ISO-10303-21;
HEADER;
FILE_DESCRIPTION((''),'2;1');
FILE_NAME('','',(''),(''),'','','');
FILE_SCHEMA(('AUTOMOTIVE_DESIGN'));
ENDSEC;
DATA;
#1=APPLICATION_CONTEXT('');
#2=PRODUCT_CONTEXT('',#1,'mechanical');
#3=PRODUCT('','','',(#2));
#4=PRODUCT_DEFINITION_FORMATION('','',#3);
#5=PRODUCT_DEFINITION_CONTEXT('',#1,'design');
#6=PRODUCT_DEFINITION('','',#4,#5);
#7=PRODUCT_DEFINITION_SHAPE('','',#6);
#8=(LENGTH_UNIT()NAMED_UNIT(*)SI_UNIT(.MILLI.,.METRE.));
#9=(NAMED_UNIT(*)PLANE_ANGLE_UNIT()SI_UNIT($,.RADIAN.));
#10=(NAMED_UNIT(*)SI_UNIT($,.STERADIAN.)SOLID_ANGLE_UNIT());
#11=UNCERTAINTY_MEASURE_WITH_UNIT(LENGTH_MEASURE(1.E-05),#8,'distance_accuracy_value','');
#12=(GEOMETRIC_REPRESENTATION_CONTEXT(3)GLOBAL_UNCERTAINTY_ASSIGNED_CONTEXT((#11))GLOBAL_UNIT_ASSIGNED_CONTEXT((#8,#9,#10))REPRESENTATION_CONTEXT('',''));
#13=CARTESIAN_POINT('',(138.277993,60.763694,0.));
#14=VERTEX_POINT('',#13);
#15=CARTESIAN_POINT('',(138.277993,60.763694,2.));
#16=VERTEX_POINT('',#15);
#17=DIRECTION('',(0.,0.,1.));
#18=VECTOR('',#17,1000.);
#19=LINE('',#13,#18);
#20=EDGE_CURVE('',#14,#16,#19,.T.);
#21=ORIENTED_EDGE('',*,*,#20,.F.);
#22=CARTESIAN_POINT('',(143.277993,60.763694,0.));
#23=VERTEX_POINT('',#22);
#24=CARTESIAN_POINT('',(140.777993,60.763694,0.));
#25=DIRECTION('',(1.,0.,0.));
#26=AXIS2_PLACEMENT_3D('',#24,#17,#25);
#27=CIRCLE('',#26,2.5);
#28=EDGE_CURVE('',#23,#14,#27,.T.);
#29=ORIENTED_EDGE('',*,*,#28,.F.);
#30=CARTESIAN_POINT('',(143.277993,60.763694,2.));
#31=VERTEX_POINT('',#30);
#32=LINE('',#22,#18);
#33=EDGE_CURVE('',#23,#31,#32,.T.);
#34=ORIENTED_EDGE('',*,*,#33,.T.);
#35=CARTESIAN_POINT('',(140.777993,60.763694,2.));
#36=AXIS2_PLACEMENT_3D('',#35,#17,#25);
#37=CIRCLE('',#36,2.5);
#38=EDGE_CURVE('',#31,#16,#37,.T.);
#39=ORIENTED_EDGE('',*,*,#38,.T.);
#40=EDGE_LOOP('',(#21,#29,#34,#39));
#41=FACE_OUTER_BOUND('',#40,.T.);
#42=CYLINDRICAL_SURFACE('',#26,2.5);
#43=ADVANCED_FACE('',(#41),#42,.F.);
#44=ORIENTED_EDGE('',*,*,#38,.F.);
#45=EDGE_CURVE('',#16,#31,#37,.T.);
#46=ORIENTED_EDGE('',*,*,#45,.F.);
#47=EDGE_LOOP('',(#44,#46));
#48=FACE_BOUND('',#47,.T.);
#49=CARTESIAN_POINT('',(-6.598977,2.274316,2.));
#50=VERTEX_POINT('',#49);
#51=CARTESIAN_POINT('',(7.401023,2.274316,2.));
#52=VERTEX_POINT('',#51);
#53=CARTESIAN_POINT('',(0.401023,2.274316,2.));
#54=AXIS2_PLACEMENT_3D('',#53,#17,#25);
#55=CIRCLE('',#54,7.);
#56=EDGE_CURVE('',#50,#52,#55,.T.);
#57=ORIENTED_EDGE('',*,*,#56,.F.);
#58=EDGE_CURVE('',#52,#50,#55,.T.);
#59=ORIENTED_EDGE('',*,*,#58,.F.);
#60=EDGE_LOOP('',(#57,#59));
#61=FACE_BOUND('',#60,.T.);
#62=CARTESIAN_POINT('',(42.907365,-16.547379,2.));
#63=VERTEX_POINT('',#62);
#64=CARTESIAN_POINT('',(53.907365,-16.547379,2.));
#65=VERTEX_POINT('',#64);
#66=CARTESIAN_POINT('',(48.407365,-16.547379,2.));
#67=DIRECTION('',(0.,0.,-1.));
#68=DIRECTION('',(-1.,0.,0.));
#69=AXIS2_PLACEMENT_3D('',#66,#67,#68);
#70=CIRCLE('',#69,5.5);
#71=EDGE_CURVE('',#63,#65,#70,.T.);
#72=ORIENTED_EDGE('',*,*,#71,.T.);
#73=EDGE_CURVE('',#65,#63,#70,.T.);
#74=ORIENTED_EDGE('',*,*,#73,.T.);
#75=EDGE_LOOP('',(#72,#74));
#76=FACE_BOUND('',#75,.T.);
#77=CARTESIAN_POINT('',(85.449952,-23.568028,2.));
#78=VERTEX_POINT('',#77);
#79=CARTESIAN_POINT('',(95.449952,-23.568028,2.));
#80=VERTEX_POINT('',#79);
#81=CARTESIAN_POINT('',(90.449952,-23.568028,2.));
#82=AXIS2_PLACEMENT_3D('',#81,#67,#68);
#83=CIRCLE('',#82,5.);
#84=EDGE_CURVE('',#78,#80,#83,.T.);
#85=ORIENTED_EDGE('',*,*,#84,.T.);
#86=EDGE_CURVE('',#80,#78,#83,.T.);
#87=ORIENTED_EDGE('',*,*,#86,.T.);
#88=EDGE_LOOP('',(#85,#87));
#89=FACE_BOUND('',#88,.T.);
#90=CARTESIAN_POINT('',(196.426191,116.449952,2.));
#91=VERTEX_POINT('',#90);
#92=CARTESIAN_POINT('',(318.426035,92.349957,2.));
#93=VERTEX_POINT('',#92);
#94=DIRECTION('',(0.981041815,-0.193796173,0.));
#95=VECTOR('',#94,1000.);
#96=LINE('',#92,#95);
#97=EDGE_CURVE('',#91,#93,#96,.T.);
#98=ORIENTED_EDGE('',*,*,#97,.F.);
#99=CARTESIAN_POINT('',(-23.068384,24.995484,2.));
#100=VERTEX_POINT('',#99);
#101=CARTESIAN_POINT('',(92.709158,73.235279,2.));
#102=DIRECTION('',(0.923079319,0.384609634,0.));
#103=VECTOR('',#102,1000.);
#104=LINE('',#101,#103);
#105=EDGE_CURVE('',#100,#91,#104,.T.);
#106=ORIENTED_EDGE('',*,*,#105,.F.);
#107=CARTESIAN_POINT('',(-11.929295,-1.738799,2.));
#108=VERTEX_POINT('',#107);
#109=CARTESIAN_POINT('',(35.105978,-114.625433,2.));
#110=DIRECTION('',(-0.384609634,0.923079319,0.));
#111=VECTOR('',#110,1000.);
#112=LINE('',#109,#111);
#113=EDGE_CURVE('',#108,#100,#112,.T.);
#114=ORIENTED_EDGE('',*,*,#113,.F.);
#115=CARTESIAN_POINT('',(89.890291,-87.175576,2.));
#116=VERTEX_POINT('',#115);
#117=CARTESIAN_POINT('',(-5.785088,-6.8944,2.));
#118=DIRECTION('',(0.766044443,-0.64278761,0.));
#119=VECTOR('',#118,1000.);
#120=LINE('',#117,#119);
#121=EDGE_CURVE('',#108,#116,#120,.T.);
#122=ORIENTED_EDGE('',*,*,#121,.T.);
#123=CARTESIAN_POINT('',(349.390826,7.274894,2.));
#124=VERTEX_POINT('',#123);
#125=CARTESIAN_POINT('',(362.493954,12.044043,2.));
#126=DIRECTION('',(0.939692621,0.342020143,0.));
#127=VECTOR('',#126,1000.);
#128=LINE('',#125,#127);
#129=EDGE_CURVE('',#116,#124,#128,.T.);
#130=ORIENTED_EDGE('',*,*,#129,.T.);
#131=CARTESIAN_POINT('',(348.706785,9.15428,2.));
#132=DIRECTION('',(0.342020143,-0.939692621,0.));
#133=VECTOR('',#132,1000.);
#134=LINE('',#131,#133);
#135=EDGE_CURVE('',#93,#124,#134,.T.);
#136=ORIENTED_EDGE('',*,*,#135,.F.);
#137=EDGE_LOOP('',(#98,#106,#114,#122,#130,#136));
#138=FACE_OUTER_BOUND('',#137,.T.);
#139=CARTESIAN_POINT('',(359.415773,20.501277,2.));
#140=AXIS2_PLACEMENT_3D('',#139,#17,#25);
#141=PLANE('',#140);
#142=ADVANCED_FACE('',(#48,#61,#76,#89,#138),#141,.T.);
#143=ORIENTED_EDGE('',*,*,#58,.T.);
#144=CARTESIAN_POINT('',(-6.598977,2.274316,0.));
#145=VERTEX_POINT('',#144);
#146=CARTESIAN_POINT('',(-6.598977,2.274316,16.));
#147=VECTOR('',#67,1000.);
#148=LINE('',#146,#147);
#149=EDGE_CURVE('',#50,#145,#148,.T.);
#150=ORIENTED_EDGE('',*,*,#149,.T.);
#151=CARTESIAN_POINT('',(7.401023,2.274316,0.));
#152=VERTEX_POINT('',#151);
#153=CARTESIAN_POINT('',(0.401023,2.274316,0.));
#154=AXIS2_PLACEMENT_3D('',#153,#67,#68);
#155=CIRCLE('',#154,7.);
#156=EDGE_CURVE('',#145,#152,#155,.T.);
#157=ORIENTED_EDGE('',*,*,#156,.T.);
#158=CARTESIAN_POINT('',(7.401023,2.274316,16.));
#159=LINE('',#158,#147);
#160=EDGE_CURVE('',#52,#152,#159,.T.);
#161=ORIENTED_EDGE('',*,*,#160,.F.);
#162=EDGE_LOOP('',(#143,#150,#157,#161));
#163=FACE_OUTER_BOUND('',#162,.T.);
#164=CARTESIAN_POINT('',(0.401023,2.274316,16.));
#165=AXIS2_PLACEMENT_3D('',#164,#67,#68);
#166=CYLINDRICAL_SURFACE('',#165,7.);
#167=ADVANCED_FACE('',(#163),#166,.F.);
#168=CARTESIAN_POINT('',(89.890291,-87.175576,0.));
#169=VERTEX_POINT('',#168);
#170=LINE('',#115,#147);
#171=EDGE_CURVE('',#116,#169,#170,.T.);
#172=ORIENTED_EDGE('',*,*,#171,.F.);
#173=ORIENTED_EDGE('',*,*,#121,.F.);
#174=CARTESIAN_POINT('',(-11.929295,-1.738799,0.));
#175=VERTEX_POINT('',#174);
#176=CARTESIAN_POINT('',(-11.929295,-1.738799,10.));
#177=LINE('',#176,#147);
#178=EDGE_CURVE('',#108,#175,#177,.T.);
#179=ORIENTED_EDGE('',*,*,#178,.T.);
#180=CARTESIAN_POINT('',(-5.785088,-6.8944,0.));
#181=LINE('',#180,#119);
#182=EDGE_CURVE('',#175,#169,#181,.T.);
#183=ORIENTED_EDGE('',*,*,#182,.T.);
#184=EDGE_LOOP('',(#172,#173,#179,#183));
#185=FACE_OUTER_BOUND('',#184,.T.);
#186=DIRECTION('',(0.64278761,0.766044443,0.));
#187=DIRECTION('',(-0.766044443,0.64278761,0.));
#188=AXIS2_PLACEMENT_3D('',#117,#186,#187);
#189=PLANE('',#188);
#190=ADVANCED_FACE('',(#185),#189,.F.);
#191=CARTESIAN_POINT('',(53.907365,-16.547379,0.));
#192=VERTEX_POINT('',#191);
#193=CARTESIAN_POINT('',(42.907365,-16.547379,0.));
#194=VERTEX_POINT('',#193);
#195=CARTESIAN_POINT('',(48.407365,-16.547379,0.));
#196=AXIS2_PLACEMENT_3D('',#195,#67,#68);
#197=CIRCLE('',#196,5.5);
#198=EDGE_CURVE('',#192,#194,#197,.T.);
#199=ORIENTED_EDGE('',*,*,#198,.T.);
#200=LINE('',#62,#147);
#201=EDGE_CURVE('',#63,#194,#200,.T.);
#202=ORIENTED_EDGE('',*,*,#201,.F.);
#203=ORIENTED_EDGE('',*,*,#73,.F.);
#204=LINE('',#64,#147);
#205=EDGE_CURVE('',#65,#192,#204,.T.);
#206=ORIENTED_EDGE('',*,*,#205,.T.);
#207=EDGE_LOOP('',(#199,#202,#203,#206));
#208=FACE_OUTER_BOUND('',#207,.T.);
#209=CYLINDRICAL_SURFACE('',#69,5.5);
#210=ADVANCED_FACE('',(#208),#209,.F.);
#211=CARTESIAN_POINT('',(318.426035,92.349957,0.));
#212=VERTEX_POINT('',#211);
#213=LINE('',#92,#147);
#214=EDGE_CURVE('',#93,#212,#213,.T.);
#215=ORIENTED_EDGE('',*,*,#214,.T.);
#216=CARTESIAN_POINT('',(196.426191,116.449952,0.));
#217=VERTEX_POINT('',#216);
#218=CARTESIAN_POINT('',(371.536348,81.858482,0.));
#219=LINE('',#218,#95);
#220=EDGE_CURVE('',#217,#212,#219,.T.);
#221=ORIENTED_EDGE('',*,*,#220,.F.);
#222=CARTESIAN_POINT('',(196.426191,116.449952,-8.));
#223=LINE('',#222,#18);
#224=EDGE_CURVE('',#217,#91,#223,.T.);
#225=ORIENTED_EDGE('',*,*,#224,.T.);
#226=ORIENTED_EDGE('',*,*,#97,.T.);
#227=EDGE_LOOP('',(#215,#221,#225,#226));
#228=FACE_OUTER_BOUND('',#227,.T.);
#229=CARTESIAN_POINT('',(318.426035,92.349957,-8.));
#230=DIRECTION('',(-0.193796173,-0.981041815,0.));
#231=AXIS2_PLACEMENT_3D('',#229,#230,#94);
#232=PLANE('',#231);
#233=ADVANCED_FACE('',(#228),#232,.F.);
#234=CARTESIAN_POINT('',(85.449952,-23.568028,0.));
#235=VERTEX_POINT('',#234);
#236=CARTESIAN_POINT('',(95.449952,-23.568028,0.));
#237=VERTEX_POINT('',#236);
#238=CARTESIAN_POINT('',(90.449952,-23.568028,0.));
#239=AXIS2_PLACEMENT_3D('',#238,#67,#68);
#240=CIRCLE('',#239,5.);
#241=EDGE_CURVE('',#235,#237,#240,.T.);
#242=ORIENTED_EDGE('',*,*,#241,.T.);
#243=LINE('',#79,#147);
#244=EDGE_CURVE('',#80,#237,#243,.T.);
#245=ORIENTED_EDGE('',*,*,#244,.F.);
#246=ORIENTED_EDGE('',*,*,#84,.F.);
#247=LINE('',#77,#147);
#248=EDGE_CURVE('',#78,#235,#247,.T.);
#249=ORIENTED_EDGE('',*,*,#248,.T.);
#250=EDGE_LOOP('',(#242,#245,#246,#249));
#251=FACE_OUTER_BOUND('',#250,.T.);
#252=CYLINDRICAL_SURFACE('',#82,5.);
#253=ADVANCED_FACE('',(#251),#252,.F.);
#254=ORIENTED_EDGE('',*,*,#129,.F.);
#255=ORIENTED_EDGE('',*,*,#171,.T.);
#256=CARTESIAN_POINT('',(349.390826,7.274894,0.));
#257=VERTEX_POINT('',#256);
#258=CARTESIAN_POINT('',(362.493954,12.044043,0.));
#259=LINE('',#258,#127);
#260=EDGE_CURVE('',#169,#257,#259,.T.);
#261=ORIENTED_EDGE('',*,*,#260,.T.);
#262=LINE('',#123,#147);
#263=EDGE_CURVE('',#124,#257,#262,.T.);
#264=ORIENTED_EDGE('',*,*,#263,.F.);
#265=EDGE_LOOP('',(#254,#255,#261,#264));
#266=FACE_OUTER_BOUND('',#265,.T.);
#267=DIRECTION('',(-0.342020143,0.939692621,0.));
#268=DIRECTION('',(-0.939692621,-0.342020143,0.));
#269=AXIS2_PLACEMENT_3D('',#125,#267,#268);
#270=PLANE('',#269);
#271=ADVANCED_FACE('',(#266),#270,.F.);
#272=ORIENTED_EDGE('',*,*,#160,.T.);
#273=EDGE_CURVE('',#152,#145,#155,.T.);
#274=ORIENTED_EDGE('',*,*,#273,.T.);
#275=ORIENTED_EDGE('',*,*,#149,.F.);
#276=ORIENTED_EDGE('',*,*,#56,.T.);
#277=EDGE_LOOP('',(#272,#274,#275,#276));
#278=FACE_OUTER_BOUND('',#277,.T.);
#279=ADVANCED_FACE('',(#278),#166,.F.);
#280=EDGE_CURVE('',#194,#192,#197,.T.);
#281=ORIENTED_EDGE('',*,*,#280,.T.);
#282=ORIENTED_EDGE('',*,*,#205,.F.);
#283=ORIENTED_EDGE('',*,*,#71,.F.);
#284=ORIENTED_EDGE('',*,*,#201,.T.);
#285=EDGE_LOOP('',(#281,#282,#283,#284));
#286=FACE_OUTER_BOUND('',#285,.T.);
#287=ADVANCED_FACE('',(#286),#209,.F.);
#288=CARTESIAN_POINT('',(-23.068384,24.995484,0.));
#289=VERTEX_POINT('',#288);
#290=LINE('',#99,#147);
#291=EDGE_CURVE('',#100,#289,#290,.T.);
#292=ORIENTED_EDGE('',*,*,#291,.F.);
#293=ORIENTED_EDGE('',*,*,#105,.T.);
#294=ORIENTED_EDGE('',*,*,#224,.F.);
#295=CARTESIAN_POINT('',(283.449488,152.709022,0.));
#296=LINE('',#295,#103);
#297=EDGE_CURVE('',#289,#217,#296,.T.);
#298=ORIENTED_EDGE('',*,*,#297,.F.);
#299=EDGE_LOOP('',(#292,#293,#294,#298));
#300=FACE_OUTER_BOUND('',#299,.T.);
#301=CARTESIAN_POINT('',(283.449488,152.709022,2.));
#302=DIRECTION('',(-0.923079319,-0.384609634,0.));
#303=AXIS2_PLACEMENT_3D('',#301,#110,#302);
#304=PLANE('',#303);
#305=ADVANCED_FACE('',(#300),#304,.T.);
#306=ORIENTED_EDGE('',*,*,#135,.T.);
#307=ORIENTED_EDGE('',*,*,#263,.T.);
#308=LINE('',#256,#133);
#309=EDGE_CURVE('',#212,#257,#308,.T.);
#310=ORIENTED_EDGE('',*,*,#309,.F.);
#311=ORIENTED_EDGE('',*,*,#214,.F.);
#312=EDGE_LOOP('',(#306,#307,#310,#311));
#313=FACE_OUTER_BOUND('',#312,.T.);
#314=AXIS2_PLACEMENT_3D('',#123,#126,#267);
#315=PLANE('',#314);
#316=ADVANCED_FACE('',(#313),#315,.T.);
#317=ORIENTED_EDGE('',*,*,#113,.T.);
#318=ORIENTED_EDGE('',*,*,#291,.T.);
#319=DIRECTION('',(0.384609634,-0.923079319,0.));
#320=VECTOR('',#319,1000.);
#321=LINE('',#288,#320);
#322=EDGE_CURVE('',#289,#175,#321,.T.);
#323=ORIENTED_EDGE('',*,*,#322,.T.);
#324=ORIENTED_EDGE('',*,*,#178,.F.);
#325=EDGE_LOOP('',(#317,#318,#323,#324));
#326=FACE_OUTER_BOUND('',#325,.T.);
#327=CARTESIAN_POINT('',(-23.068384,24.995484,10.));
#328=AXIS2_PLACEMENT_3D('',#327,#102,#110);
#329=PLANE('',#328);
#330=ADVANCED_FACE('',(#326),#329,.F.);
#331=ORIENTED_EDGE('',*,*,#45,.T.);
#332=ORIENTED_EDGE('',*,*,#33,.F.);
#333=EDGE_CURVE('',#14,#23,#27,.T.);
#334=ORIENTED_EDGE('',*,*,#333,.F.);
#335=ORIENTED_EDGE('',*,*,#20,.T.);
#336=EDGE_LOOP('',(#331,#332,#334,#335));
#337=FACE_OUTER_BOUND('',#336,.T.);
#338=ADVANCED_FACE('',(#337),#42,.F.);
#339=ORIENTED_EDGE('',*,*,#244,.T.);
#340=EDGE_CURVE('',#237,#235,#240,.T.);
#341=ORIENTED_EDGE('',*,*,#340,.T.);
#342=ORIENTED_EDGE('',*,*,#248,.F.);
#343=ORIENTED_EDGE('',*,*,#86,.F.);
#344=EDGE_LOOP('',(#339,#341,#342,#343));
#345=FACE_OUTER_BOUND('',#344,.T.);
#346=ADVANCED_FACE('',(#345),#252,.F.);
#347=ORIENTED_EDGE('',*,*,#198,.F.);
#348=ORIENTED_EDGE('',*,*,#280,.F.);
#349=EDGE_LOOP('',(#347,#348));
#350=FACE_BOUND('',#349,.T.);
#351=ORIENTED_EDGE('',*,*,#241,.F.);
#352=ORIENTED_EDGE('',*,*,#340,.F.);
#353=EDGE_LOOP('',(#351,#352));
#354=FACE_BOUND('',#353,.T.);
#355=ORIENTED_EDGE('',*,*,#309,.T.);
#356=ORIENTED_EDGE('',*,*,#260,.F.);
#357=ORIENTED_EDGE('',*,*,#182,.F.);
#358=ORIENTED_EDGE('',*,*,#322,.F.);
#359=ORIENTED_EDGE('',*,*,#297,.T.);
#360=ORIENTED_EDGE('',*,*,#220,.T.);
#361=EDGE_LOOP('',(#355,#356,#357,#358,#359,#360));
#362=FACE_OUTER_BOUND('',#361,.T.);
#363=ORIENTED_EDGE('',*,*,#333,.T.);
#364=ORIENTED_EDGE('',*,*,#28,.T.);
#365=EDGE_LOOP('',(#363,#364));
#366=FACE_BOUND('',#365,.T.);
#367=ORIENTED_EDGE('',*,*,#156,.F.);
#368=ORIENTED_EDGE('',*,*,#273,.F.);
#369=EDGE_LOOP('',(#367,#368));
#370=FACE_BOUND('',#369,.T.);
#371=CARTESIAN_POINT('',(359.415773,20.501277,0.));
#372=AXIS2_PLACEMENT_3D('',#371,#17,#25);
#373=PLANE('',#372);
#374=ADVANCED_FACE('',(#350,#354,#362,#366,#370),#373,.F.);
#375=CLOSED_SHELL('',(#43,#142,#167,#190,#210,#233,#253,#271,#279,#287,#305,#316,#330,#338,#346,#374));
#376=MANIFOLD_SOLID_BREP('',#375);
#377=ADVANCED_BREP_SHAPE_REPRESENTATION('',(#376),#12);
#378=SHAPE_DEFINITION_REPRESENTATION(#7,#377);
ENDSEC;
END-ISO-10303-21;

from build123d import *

# Parameters (mm, degrees)
SKETCH_1_R          = 3
EXTRUDE_1_DEPTH     = 2
EXTRUDE_2_DEPTH     = 2
SKETCH_4_OUTSIDE_W  = 464.3
SKETCH_4_OUTSIDE_H  = 281.017
CUT_EXTRUDE_1_DEPTH = 10
EXTRUDE_3_DEPTH     = 2
SKETCH_6_R          = 7
CUT_EXTRUDE_2_DEPTH = 16
EXTRUDE_4_DEPTH     = 2
CUT_EXTRUDE_3_DEPTH = 10
CUT_EXTRUDE_4_DEPTH = 10
SKETCH_10_R         = 2.5
CUT_EXTRUDE_5_DEPTH = 369.29137958
SKETCH_11_R         = 5.5
CUT_EXTRUDE_6_DEPTH = 369.29137958
SKETCH_13_R         = 5
CUT_EXTRUDE_7_DEPTH = 369.29137958


with BuildPart() as part:
    # 草图1 → 凸台-拉伸1 (new body)
    with BuildSketch(Plane.XY):
        with BuildLine():
            Line((362.493953978, 12.044043029), (89.890291348, -87.17557592))
            Line((89.890291348, -87.17557592), (-5.785088487, -6.894399988))
            ThreePointArc((-5.785088487, -6.894399988), (-6.894399988, 5.785088487), (5.785088487, 6.894399988))
            Line((5.785088487, 6.894399988), (93.499500944, -66.706731154))
            Line((93.499500944, -66.706731154), (356.337591398, 28.958510203))
            ThreePointArc((356.337591398, 28.958510203), (367.873006275, 23.579457906), (362.493953978, 12.044043029))
        make_face()
        with Locations((359.415772688, 20.501276616)):
            Circle(SKETCH_1_R, mode=Mode.SUBTRACT)
        Circle(SKETCH_1_R, mode=Mode.SUBTRACT)
    extrude(amount=EXTRUDE_1_DEPTH)

    # 草图3 → 凸台-拉伸2 (add)
    with BuildSketch(Plane.XY.offset(2)):
        Polygon((24.555501063, -8.855846282), (93.499500944, -66.706731154), (337.819582349, 22.218506111), (302.512305891, 106.957456662), align=None)
    extrude(amount=-EXTRUDE_2_DEPTH)

    # 草图4 outside → 切除-拉伸1 (cut)
    with BuildSketch(Plane(origin=(0, 0, 0), x_dir=(-1, 0, 0), z_dir=(0, 0, -1))):
        with Locations((-179.708, 9.8905)):
            Rectangle(SKETCH_4_OUTSIDE_W, SKETCH_4_OUTSIDE_H)
        Polygon((-337.819582349, 22.218506111), (-344.749797365, 5.585698189), (-89.890291348, -87.17557592), (-5.843844232, -16.652233143), (-24.555501063, -8.855846282), (-302.512305891, 106.957456662), align=None, mode=Mode.SUBTRACT)
    extrude(amount=-CUT_EXTRUDE_1_DEPTH, mode=Mode.SUBTRACT)

    # 草图5 → 凸台-拉伸3 (add)
    with BuildSketch(Plane(origin=(0, 0, 0), x_dir=(-1, 0, 0), z_dir=(0, 0, -1))):
        Polygon((-302.512305891, 106.957456662), (-283.449488043, 152.709022376), (-92.70915772, 73.235279423), (36.914573348, 19.226339278), (-5.843844232, -16.652233143), align=None)
    extrude(amount=-EXTRUDE_3_DEPTH)

    # 草图6 → 切除-拉伸2 (cut)
    with BuildSketch(Plane(origin=(0, 0, 0), x_dir=(-1, 0, 0), z_dir=(0, 0, -1))):
        with Locations((-0.401023288, 2.274316085)):
            Circle(SKETCH_6_R)
    extrude(amount=-CUT_EXTRUDE_2_DEPTH, mode=Mode.SUBTRACT)

    # 草图7 → 凸台-拉伸4 (add)
    with BuildSketch(Plane(origin=(0, 0, 0), x_dir=(-1, 0, 0), z_dir=(0, 0, -1))):
        Polygon((-344.749797365, 5.585698189), (-349.390825639, 7.274894338), (-348.706785352, 9.154279579), (-294.744261489, 157.415095392), (-283.449488043, 152.709022376), align=None)
    extrude(amount=-EXTRUDE_4_DEPTH)

    # 草图8 → 切除-拉伸3 (cut)
    with BuildSketch(Plane.XY.offset(2)):
        Polygon((318.426035297, 92.349956602), (196.426191084, 116.449951619), (294.744261489, 157.415095392), align=None)
    extrude(amount=-CUT_EXTRUDE_3_DEPTH, mode=Mode.SUBTRACT)

    # 草图9 → 切除-拉伸4 (cut)
    with BuildSketch(Plane(origin=(0, 0, 0), x_dir=(-1, 0, 0), z_dir=(0, 0, -1))):
        Polygon((23.068383558, 24.995483781), (11.929294577, -1.738798924), (36.914573348, 19.226339278), align=None)
    extrude(amount=-CUT_EXTRUDE_4_DEPTH, mode=Mode.SUBTRACT)

    # 草图10 → 切除-拉伸5 (cut, through all)
    with BuildSketch(Plane.XY.offset(2)):
        with Locations((140.777993137, 60.76369374)):
            Circle(SKETCH_10_R)
    extrude(amount=-CUT_EXTRUDE_5_DEPTH, mode=Mode.SUBTRACT)

    # 草图11 → 切除-拉伸6 (cut, through all)
    with BuildSketch(Plane(origin=(0, 0, 0), x_dir=(-1, 0, 0), z_dir=(0, 0, -1))):
        with Locations((-48.407364973, -16.547379186)):
            Circle(SKETCH_11_R)
    extrude(amount=-CUT_EXTRUDE_6_DEPTH, mode=Mode.SUBTRACT)

    # 草图13 → 切除-拉伸7 (cut, through all)
    with BuildSketch(Plane(origin=(0, 0, 0), x_dir=(-1, 0, 0), z_dir=(0, 0, -1))):
        with Locations((-90.449951862, -23.568027643)):
            Circle(SKETCH_13_R)
    extrude(amount=-CUT_EXTRUDE_7_DEPTH, mode=Mode.SUBTRACT)


solid = part.part
